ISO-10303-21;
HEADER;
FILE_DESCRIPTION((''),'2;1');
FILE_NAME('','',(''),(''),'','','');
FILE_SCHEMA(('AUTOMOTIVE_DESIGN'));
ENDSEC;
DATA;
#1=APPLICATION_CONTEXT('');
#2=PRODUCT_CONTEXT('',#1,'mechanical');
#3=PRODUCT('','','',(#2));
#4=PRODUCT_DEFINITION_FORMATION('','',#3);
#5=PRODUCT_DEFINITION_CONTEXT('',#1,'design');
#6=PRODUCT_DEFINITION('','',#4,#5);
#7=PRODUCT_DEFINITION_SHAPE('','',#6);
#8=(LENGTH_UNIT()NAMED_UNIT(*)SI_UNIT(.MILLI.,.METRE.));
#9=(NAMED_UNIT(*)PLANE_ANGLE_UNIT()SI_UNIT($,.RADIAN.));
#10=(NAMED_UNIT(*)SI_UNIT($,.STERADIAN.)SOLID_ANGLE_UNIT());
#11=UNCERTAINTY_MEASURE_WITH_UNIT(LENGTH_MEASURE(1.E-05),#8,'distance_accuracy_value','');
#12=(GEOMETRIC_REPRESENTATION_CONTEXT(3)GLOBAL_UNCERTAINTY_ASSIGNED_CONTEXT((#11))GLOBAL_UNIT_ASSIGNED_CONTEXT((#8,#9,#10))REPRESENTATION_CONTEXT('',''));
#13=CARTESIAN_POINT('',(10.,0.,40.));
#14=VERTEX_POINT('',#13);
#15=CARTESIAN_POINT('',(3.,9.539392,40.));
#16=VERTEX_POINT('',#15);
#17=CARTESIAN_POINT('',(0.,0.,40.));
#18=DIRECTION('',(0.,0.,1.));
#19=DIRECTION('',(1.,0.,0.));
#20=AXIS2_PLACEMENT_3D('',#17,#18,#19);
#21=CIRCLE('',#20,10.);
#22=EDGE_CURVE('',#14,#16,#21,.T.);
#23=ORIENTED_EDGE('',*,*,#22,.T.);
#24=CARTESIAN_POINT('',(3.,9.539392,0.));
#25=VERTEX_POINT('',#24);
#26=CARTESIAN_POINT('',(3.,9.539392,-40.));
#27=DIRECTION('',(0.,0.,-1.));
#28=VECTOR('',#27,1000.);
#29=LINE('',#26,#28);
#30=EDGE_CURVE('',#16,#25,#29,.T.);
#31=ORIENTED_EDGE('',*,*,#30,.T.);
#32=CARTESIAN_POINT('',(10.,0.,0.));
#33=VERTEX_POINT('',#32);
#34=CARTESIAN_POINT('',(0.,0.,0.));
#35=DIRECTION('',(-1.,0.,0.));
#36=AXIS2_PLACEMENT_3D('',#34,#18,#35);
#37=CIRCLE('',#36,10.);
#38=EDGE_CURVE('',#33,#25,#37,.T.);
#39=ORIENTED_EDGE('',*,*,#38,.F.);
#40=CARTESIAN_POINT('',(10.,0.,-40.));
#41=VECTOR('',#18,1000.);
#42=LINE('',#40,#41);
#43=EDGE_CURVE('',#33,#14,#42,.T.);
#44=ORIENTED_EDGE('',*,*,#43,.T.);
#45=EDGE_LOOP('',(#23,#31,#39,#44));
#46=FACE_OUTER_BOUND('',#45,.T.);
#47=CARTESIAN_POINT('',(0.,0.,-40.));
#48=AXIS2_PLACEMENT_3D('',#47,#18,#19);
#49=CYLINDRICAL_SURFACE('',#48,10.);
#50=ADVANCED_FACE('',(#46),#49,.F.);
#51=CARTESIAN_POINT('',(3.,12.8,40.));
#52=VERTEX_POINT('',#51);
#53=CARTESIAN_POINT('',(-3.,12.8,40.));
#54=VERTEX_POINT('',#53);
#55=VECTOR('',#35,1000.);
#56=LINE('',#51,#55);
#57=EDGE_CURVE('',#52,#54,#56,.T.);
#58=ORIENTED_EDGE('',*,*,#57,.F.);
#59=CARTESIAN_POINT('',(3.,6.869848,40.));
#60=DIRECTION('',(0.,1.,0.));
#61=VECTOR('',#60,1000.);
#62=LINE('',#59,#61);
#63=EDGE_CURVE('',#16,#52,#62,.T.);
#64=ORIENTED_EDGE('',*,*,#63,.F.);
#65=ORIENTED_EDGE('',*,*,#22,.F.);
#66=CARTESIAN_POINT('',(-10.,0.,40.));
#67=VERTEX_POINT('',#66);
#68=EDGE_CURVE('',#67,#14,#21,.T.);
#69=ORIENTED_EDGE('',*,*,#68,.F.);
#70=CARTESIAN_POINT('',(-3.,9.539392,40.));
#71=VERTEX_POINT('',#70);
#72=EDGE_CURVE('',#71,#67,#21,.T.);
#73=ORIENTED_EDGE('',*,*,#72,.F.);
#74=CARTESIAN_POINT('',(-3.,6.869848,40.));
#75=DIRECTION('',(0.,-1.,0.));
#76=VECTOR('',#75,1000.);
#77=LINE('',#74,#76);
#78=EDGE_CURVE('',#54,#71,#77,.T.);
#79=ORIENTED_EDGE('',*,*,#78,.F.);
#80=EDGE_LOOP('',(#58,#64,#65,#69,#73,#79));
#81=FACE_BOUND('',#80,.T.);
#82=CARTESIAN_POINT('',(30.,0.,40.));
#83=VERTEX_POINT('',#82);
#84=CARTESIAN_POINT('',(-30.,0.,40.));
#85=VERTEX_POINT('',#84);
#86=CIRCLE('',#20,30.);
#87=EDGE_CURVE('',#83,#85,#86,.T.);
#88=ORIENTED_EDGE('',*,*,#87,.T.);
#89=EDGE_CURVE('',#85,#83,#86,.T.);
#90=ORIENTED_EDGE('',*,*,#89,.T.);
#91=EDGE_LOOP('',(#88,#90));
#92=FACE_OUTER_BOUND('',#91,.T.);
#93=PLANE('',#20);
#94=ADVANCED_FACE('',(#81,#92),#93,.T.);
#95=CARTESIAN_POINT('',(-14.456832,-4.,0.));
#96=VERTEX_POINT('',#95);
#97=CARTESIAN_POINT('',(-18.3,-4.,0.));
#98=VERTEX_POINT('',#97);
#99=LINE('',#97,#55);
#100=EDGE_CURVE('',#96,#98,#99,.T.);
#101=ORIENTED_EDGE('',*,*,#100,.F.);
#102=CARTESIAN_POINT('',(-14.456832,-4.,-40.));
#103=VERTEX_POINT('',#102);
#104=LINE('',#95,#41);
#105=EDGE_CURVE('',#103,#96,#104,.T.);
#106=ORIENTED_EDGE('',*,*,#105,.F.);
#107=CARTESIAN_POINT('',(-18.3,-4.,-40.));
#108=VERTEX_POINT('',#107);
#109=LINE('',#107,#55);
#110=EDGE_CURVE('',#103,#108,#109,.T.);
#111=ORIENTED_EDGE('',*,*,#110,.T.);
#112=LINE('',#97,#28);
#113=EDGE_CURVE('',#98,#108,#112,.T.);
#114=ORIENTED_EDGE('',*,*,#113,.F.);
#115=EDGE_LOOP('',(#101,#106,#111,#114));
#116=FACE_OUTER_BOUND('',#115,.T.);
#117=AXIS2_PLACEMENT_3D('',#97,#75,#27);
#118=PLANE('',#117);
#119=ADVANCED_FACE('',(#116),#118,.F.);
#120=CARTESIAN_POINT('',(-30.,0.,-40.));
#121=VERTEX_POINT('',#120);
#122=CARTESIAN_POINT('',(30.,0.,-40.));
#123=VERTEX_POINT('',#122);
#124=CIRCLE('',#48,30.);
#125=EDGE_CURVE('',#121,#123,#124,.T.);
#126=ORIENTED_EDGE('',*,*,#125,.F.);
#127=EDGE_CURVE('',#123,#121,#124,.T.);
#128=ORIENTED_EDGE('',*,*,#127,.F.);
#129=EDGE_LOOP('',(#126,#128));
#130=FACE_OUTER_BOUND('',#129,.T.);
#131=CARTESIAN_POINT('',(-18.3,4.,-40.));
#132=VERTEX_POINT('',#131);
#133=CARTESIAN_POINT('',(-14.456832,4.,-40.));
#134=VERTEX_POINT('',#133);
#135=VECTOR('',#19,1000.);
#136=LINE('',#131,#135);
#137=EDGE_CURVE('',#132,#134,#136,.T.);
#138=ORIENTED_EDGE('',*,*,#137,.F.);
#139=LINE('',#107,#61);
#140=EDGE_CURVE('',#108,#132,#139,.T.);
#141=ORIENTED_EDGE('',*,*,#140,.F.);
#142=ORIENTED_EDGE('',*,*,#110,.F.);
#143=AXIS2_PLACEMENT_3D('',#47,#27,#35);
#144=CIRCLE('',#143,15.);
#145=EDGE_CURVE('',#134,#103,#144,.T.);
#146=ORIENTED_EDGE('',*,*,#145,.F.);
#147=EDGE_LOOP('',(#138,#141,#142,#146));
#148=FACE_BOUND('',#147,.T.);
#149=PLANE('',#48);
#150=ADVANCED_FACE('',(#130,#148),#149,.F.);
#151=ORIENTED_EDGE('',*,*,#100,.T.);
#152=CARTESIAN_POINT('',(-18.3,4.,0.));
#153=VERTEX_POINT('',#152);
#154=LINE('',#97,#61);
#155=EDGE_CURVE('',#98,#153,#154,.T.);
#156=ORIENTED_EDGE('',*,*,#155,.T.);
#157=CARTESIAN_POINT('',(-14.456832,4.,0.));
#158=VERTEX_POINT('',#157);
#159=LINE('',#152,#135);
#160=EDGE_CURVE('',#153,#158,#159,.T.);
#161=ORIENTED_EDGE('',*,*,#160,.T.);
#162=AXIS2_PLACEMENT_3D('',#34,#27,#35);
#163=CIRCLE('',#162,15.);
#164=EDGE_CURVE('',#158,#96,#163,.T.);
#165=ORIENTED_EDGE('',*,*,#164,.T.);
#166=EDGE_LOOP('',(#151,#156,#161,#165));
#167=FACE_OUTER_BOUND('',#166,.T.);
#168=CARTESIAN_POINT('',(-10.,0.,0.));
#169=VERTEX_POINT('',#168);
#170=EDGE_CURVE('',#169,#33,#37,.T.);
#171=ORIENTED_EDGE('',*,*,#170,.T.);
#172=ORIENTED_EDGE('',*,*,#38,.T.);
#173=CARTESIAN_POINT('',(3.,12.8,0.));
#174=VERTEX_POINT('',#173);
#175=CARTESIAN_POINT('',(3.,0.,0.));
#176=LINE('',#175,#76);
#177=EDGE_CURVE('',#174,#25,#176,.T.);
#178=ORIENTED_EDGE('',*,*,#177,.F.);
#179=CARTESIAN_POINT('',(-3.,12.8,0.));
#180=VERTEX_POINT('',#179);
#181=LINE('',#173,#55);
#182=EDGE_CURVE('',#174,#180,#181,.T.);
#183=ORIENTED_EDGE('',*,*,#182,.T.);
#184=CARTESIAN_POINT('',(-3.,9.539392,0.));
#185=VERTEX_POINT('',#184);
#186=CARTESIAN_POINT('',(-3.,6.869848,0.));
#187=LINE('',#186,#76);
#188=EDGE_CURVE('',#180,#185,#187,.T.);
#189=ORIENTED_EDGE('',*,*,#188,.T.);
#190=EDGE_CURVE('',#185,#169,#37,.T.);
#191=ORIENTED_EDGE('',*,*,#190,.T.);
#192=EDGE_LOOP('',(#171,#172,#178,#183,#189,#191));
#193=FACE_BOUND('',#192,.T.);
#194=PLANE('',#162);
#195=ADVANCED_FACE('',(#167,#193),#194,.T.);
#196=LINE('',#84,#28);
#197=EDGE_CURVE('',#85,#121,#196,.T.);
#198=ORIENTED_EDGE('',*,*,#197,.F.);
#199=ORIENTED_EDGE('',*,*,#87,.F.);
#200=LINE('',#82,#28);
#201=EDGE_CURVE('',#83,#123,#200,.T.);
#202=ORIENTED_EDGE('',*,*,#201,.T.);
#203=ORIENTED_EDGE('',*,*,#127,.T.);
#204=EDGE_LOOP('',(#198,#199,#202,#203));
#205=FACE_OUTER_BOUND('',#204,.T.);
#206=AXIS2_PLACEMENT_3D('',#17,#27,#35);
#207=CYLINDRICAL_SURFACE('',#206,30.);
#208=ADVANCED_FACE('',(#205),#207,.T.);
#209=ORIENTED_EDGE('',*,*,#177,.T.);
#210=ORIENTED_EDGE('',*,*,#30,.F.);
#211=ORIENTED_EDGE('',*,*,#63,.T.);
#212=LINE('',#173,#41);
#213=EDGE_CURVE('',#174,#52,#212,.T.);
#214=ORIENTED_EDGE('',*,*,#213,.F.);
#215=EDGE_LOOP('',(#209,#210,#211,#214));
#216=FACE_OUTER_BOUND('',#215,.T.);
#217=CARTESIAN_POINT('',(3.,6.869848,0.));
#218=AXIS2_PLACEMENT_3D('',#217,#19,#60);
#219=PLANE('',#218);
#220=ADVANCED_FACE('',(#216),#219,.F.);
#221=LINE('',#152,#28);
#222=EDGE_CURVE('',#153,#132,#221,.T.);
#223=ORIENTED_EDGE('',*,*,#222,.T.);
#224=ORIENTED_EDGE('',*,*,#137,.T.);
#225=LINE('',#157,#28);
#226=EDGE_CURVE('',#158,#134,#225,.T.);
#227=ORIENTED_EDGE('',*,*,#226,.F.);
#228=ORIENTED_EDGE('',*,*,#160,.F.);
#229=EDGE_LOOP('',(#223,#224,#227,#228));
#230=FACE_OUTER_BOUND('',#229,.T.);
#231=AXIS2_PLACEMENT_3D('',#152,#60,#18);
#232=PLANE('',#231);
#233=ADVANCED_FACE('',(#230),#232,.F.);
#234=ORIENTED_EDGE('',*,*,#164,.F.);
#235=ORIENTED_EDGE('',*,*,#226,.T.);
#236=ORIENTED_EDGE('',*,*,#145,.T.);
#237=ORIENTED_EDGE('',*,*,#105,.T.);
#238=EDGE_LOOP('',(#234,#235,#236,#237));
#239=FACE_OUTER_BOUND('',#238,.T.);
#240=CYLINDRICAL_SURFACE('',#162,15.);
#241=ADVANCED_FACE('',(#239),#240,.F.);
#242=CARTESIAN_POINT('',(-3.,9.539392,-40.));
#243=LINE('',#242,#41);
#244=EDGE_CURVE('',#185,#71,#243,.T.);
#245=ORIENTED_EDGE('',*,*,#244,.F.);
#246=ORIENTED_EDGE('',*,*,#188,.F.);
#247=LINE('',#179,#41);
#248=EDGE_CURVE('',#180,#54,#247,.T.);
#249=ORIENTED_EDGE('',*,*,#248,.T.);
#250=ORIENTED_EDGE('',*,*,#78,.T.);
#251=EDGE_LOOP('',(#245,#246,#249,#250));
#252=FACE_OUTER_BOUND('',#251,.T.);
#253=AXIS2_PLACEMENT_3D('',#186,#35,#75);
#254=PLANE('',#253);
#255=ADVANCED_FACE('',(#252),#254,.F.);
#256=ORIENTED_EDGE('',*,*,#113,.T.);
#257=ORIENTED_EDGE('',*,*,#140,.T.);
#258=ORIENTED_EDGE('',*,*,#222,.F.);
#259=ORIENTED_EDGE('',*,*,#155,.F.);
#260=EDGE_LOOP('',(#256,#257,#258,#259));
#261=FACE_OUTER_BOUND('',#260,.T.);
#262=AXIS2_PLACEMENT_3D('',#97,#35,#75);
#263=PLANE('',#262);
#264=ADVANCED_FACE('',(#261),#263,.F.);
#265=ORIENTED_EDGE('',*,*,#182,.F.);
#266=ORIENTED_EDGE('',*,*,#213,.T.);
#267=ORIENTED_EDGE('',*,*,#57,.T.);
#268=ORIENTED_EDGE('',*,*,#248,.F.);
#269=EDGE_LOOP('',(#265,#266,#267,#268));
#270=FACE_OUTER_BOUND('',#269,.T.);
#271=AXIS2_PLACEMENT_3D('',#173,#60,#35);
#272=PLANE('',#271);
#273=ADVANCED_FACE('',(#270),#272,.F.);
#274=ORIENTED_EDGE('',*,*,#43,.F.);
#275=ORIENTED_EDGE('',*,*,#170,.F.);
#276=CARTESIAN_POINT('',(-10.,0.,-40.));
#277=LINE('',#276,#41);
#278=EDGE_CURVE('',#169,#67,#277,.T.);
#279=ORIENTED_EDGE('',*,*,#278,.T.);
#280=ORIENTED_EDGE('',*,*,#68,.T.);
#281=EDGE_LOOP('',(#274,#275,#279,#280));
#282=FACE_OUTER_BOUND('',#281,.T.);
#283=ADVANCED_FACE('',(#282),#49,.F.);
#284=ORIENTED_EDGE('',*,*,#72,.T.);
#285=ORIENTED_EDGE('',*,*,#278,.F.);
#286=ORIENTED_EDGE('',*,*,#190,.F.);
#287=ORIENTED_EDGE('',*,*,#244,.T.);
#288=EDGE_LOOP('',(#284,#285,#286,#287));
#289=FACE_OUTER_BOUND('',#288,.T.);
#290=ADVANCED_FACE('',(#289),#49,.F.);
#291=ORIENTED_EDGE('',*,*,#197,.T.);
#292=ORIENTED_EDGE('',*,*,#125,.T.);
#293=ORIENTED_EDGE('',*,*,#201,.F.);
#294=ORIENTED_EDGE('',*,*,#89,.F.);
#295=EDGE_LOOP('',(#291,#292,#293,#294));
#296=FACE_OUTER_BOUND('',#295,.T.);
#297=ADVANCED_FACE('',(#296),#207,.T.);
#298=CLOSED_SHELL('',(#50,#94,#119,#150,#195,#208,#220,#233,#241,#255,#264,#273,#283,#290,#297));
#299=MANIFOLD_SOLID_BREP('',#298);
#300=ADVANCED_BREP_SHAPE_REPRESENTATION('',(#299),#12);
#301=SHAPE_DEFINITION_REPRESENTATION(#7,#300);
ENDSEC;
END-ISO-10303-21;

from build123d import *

# Parameters (mm, degrees)
SKETCH1_R           = 30
BOSS_EXTRUDE1_DEPTH = 40
SKETCH2_R           = 10
CUT_EXTRUDE1_DEPTH  = 91.553851381
SKETCH3_R           = 15
CUT_EXTRUDE2_DEPTH  = 40
SKETCH4_W           = 6
SKETCH4_H           = 5.930152299
CUT_EXTRUDE3_DEPTH  = 40
SKETCH5_W           = 6.6
SKETCH5_H           = 8
CUT_EXTRUDE4_DEPTH  = 40


with BuildPart() as part:
    # Sketch1 → Boss-Extrude1 (new, symmetric)
    with BuildSketch(Plane.XY):
        Circle(SKETCH1_R)
    extrude(amount=BOSS_EXTRUDE1_DEPTH, both=True)

    # Sketch2 → Cut-Extrude1 (cut, through all)
    with BuildSketch(Plane.XY.offset(40)):
        Circle(SKETCH2_R)
    extrude(amount=-CUT_EXTRUDE1_DEPTH, mode=Mode.SUBTRACT)

    # Sketch3 → Cut-Extrude2 (cut)
    with BuildSketch(Plane(origin=(0, 0, -40), x_dir=(-1, 0, 0), z_dir=(0, 0, -1))):
        Circle(SKETCH3_R)
    extrude(amount=-CUT_EXTRUDE2_DEPTH, mode=Mode.SUBTRACT)

    # Sketch4 → Cut-Extrude3 (cut)
    with BuildSketch(Plane.XY.offset(40)):
        with Locations((0, 9.834923851)):
            Rectangle(SKETCH4_W, SKETCH4_H)
    extrude(amount=-CUT_EXTRUDE3_DEPTH, mode=Mode.SUBTRACT)

    # Sketch5 → Cut-Extrude4 (cut)
    with BuildSketch(Plane(origin=(0, 0, -40), x_dir=(-1, 0, 0), z_dir=(0, 0, -1))):
        with Locations((15, 0)):
            Rectangle(SKETCH5_W, SKETCH5_H)
    extrude(amount=-CUT_EXTRUDE4_DEPTH, mode=Mode.SUBTRACT)


solid = part.part
